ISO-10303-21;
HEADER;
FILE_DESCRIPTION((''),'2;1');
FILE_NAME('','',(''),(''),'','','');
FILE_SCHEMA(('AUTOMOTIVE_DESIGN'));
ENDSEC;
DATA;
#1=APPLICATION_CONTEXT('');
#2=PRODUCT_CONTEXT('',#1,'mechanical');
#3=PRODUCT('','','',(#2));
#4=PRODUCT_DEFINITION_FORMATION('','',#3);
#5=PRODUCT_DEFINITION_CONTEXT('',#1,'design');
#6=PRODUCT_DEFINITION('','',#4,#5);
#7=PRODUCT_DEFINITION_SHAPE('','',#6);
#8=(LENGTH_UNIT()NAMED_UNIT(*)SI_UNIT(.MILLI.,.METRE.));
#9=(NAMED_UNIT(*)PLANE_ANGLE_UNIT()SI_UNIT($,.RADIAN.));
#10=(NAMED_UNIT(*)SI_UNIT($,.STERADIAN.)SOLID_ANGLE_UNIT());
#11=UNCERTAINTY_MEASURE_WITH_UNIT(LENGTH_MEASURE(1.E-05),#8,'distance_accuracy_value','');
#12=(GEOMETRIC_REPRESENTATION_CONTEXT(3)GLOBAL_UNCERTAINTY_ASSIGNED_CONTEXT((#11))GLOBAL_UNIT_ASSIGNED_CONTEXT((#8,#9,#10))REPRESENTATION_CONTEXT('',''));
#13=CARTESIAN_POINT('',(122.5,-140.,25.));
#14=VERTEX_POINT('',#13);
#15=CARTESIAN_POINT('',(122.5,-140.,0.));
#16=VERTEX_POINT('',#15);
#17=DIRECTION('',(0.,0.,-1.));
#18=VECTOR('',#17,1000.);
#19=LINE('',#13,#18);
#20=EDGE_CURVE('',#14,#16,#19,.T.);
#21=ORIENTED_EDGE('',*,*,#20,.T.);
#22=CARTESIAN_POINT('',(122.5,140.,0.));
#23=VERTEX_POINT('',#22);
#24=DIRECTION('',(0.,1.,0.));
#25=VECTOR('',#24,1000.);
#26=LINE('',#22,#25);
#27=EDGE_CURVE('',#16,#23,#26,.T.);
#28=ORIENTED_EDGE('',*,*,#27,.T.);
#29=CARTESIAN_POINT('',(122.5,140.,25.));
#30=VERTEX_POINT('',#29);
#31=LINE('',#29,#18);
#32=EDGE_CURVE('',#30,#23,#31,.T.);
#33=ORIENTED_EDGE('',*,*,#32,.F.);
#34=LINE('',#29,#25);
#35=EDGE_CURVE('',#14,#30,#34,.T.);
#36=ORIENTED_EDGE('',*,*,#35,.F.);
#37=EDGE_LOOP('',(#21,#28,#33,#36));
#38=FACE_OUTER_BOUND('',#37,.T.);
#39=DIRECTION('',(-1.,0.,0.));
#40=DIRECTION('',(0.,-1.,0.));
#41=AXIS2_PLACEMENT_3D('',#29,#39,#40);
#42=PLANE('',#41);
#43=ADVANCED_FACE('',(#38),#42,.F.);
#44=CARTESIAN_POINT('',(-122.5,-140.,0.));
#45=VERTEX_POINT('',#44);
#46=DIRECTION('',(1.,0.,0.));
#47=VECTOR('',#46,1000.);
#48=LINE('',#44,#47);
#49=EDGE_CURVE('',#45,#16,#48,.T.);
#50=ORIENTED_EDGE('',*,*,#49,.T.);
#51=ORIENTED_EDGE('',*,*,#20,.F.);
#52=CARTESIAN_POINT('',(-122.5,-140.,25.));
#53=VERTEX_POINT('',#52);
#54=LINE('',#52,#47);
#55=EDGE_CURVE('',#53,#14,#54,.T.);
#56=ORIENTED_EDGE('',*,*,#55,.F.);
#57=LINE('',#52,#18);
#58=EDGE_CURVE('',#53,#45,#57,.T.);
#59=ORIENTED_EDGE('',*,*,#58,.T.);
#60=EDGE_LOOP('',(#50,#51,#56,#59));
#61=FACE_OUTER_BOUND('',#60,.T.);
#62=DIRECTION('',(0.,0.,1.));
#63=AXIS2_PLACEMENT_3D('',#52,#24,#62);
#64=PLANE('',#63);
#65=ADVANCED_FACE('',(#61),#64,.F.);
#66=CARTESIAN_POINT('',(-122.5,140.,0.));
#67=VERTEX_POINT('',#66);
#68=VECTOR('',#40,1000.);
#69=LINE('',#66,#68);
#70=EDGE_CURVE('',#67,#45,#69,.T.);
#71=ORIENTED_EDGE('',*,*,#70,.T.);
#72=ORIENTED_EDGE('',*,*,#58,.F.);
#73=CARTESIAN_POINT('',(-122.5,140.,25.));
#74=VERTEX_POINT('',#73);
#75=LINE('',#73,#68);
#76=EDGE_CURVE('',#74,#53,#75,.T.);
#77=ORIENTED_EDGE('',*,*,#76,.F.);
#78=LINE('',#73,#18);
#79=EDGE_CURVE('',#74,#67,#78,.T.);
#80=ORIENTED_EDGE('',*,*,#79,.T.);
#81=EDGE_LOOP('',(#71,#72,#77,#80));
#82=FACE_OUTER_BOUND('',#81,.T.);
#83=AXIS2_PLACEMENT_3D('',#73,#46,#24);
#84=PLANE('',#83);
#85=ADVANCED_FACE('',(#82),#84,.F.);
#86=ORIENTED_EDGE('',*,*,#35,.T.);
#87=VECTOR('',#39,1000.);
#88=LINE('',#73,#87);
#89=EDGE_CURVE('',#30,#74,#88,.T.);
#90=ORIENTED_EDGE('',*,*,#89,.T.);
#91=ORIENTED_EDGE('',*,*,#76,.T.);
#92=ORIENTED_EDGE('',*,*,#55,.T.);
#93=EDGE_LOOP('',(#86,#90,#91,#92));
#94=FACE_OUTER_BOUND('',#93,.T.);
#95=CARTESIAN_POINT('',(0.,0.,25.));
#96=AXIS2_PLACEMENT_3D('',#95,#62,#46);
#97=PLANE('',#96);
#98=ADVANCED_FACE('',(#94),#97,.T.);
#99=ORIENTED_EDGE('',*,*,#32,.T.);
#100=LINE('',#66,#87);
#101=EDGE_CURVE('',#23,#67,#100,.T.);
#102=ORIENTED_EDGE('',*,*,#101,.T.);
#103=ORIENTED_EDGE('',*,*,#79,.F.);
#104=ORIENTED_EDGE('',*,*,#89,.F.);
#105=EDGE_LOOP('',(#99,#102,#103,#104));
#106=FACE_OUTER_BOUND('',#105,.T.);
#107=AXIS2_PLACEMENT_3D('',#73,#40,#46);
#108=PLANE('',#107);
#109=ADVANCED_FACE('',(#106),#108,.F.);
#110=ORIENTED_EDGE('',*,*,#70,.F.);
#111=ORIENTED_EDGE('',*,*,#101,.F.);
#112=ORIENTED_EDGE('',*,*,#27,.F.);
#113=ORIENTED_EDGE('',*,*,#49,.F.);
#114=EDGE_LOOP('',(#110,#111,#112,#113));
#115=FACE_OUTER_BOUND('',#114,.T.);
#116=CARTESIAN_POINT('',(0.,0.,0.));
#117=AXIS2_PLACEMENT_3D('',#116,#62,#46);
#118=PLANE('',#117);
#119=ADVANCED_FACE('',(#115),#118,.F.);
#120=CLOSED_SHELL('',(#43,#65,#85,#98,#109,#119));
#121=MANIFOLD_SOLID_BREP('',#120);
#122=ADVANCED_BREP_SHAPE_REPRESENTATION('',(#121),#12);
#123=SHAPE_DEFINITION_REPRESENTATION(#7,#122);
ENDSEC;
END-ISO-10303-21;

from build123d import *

# Parameters (mm, degrees)
SKETCH_1_W      = 245
SKETCH_1_H      = 280
EXTRUDE_1_DEPTH = 25


with BuildPart() as part:
    # 草图1 → 凸台-拉伸1 (new body)
    with BuildSketch(Plane.XY):
        Rectangle(SKETCH_1_W, SKETCH_1_H)
    extrude(amount=EXTRUDE_1_DEPTH)


solid = part.part
